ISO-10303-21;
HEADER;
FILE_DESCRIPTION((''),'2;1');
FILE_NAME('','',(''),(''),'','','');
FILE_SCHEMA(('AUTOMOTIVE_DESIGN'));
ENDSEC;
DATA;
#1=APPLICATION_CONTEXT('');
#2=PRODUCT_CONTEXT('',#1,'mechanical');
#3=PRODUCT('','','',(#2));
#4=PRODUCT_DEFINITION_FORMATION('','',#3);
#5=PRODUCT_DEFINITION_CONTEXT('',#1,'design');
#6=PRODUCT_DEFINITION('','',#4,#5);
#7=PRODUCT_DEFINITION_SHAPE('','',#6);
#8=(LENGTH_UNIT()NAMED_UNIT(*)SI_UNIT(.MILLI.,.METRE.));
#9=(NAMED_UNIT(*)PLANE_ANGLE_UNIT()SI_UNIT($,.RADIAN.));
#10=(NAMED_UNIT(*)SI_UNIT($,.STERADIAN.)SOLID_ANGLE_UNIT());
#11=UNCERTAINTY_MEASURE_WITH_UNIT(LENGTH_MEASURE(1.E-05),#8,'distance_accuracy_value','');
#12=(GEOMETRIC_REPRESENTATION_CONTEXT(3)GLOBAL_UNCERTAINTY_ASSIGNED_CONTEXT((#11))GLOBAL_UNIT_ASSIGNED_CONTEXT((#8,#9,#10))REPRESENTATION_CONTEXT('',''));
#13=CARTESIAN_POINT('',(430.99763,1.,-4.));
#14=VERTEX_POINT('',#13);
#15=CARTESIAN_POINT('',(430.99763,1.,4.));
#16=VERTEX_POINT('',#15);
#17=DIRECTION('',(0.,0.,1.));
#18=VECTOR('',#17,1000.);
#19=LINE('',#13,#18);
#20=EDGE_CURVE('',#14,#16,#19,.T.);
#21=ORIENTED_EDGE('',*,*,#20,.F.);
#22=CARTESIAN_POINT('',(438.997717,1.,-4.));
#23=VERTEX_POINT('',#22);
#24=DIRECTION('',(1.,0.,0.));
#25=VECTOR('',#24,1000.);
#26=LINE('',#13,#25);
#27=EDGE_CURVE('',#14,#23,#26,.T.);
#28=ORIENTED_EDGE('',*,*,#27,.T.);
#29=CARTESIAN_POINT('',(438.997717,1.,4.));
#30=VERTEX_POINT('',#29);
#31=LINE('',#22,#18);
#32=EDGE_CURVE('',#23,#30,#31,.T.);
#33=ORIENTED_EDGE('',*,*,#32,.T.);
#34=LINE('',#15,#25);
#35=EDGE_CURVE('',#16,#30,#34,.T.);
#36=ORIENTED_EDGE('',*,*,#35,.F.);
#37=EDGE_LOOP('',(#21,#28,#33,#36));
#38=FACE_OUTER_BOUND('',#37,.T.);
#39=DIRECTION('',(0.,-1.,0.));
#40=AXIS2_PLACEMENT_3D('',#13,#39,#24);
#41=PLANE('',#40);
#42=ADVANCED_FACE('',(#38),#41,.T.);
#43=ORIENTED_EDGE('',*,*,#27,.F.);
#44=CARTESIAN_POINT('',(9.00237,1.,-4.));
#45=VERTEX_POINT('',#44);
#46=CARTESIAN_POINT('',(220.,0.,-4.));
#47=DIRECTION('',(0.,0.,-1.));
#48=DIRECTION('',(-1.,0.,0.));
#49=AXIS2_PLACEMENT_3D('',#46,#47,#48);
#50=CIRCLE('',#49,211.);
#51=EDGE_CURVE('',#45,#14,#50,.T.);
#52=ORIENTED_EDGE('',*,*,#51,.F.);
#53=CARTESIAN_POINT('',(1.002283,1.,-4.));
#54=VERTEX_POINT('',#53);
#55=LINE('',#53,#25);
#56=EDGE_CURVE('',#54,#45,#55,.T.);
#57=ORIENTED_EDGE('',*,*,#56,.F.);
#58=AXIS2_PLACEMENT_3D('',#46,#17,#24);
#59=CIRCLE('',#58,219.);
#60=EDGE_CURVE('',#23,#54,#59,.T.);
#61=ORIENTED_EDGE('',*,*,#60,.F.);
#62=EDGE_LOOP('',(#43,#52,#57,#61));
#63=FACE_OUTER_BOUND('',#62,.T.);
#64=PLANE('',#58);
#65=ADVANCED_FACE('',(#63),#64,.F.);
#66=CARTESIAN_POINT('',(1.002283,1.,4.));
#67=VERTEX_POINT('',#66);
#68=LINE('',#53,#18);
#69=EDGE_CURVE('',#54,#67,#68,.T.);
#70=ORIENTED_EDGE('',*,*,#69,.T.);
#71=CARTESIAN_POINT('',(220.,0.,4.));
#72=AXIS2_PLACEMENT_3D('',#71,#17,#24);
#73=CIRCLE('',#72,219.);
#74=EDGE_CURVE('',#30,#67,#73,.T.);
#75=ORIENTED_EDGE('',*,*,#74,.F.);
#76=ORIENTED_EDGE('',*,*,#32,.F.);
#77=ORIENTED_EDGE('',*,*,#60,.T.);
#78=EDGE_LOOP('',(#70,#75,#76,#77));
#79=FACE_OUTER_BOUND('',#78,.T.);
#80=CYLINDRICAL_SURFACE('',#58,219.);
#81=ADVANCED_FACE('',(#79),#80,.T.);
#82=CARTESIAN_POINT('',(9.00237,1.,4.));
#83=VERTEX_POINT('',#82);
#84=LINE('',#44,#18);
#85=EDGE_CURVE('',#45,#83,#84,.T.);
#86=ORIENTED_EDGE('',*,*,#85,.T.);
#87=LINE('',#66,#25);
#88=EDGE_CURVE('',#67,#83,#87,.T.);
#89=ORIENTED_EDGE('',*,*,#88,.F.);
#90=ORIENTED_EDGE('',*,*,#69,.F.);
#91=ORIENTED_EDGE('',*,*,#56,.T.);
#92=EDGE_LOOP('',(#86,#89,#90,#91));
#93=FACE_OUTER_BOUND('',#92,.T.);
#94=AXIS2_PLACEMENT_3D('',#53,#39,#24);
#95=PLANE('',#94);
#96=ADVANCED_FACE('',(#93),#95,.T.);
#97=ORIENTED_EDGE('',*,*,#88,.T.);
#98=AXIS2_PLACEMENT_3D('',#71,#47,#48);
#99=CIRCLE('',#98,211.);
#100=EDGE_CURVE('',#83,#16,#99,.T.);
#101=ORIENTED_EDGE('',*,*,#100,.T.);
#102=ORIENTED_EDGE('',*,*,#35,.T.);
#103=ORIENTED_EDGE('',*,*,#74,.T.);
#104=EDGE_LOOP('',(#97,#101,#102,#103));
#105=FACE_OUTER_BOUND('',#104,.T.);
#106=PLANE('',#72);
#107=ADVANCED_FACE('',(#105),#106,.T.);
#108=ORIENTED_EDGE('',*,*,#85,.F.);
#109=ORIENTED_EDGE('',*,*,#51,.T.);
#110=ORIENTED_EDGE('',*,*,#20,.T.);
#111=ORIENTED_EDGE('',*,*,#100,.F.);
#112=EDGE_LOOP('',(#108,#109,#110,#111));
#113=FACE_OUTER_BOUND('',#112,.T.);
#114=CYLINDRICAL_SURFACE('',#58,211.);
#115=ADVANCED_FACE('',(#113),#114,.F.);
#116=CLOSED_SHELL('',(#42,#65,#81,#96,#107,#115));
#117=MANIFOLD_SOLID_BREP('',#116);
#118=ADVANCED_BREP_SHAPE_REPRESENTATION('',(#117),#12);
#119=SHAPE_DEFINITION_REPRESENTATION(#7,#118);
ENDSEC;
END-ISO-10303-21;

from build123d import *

# Parameters (mm, degrees)
EXTRUDE_1_DEPTH = 4


with BuildPart() as part:
    # 草图1 → 凸台-拉伸1 (new, symmetric)
    with BuildSketch(Plane.XY):
        with BuildLine():
            Line((1.002283117, 1), (9.002369682, 1))
            ThreePointArc((9.002369682, 1), (220, 211), (430.997630318, 1))
            Line((430.997630318, 1), (438.997716883, 1))
            ThreePointArc((438.997716883, 1), (220, 219), (1.002283117, 1))
        make_face()
    extrude(amount=EXTRUDE_1_DEPTH, both=True)


solid = part.part
